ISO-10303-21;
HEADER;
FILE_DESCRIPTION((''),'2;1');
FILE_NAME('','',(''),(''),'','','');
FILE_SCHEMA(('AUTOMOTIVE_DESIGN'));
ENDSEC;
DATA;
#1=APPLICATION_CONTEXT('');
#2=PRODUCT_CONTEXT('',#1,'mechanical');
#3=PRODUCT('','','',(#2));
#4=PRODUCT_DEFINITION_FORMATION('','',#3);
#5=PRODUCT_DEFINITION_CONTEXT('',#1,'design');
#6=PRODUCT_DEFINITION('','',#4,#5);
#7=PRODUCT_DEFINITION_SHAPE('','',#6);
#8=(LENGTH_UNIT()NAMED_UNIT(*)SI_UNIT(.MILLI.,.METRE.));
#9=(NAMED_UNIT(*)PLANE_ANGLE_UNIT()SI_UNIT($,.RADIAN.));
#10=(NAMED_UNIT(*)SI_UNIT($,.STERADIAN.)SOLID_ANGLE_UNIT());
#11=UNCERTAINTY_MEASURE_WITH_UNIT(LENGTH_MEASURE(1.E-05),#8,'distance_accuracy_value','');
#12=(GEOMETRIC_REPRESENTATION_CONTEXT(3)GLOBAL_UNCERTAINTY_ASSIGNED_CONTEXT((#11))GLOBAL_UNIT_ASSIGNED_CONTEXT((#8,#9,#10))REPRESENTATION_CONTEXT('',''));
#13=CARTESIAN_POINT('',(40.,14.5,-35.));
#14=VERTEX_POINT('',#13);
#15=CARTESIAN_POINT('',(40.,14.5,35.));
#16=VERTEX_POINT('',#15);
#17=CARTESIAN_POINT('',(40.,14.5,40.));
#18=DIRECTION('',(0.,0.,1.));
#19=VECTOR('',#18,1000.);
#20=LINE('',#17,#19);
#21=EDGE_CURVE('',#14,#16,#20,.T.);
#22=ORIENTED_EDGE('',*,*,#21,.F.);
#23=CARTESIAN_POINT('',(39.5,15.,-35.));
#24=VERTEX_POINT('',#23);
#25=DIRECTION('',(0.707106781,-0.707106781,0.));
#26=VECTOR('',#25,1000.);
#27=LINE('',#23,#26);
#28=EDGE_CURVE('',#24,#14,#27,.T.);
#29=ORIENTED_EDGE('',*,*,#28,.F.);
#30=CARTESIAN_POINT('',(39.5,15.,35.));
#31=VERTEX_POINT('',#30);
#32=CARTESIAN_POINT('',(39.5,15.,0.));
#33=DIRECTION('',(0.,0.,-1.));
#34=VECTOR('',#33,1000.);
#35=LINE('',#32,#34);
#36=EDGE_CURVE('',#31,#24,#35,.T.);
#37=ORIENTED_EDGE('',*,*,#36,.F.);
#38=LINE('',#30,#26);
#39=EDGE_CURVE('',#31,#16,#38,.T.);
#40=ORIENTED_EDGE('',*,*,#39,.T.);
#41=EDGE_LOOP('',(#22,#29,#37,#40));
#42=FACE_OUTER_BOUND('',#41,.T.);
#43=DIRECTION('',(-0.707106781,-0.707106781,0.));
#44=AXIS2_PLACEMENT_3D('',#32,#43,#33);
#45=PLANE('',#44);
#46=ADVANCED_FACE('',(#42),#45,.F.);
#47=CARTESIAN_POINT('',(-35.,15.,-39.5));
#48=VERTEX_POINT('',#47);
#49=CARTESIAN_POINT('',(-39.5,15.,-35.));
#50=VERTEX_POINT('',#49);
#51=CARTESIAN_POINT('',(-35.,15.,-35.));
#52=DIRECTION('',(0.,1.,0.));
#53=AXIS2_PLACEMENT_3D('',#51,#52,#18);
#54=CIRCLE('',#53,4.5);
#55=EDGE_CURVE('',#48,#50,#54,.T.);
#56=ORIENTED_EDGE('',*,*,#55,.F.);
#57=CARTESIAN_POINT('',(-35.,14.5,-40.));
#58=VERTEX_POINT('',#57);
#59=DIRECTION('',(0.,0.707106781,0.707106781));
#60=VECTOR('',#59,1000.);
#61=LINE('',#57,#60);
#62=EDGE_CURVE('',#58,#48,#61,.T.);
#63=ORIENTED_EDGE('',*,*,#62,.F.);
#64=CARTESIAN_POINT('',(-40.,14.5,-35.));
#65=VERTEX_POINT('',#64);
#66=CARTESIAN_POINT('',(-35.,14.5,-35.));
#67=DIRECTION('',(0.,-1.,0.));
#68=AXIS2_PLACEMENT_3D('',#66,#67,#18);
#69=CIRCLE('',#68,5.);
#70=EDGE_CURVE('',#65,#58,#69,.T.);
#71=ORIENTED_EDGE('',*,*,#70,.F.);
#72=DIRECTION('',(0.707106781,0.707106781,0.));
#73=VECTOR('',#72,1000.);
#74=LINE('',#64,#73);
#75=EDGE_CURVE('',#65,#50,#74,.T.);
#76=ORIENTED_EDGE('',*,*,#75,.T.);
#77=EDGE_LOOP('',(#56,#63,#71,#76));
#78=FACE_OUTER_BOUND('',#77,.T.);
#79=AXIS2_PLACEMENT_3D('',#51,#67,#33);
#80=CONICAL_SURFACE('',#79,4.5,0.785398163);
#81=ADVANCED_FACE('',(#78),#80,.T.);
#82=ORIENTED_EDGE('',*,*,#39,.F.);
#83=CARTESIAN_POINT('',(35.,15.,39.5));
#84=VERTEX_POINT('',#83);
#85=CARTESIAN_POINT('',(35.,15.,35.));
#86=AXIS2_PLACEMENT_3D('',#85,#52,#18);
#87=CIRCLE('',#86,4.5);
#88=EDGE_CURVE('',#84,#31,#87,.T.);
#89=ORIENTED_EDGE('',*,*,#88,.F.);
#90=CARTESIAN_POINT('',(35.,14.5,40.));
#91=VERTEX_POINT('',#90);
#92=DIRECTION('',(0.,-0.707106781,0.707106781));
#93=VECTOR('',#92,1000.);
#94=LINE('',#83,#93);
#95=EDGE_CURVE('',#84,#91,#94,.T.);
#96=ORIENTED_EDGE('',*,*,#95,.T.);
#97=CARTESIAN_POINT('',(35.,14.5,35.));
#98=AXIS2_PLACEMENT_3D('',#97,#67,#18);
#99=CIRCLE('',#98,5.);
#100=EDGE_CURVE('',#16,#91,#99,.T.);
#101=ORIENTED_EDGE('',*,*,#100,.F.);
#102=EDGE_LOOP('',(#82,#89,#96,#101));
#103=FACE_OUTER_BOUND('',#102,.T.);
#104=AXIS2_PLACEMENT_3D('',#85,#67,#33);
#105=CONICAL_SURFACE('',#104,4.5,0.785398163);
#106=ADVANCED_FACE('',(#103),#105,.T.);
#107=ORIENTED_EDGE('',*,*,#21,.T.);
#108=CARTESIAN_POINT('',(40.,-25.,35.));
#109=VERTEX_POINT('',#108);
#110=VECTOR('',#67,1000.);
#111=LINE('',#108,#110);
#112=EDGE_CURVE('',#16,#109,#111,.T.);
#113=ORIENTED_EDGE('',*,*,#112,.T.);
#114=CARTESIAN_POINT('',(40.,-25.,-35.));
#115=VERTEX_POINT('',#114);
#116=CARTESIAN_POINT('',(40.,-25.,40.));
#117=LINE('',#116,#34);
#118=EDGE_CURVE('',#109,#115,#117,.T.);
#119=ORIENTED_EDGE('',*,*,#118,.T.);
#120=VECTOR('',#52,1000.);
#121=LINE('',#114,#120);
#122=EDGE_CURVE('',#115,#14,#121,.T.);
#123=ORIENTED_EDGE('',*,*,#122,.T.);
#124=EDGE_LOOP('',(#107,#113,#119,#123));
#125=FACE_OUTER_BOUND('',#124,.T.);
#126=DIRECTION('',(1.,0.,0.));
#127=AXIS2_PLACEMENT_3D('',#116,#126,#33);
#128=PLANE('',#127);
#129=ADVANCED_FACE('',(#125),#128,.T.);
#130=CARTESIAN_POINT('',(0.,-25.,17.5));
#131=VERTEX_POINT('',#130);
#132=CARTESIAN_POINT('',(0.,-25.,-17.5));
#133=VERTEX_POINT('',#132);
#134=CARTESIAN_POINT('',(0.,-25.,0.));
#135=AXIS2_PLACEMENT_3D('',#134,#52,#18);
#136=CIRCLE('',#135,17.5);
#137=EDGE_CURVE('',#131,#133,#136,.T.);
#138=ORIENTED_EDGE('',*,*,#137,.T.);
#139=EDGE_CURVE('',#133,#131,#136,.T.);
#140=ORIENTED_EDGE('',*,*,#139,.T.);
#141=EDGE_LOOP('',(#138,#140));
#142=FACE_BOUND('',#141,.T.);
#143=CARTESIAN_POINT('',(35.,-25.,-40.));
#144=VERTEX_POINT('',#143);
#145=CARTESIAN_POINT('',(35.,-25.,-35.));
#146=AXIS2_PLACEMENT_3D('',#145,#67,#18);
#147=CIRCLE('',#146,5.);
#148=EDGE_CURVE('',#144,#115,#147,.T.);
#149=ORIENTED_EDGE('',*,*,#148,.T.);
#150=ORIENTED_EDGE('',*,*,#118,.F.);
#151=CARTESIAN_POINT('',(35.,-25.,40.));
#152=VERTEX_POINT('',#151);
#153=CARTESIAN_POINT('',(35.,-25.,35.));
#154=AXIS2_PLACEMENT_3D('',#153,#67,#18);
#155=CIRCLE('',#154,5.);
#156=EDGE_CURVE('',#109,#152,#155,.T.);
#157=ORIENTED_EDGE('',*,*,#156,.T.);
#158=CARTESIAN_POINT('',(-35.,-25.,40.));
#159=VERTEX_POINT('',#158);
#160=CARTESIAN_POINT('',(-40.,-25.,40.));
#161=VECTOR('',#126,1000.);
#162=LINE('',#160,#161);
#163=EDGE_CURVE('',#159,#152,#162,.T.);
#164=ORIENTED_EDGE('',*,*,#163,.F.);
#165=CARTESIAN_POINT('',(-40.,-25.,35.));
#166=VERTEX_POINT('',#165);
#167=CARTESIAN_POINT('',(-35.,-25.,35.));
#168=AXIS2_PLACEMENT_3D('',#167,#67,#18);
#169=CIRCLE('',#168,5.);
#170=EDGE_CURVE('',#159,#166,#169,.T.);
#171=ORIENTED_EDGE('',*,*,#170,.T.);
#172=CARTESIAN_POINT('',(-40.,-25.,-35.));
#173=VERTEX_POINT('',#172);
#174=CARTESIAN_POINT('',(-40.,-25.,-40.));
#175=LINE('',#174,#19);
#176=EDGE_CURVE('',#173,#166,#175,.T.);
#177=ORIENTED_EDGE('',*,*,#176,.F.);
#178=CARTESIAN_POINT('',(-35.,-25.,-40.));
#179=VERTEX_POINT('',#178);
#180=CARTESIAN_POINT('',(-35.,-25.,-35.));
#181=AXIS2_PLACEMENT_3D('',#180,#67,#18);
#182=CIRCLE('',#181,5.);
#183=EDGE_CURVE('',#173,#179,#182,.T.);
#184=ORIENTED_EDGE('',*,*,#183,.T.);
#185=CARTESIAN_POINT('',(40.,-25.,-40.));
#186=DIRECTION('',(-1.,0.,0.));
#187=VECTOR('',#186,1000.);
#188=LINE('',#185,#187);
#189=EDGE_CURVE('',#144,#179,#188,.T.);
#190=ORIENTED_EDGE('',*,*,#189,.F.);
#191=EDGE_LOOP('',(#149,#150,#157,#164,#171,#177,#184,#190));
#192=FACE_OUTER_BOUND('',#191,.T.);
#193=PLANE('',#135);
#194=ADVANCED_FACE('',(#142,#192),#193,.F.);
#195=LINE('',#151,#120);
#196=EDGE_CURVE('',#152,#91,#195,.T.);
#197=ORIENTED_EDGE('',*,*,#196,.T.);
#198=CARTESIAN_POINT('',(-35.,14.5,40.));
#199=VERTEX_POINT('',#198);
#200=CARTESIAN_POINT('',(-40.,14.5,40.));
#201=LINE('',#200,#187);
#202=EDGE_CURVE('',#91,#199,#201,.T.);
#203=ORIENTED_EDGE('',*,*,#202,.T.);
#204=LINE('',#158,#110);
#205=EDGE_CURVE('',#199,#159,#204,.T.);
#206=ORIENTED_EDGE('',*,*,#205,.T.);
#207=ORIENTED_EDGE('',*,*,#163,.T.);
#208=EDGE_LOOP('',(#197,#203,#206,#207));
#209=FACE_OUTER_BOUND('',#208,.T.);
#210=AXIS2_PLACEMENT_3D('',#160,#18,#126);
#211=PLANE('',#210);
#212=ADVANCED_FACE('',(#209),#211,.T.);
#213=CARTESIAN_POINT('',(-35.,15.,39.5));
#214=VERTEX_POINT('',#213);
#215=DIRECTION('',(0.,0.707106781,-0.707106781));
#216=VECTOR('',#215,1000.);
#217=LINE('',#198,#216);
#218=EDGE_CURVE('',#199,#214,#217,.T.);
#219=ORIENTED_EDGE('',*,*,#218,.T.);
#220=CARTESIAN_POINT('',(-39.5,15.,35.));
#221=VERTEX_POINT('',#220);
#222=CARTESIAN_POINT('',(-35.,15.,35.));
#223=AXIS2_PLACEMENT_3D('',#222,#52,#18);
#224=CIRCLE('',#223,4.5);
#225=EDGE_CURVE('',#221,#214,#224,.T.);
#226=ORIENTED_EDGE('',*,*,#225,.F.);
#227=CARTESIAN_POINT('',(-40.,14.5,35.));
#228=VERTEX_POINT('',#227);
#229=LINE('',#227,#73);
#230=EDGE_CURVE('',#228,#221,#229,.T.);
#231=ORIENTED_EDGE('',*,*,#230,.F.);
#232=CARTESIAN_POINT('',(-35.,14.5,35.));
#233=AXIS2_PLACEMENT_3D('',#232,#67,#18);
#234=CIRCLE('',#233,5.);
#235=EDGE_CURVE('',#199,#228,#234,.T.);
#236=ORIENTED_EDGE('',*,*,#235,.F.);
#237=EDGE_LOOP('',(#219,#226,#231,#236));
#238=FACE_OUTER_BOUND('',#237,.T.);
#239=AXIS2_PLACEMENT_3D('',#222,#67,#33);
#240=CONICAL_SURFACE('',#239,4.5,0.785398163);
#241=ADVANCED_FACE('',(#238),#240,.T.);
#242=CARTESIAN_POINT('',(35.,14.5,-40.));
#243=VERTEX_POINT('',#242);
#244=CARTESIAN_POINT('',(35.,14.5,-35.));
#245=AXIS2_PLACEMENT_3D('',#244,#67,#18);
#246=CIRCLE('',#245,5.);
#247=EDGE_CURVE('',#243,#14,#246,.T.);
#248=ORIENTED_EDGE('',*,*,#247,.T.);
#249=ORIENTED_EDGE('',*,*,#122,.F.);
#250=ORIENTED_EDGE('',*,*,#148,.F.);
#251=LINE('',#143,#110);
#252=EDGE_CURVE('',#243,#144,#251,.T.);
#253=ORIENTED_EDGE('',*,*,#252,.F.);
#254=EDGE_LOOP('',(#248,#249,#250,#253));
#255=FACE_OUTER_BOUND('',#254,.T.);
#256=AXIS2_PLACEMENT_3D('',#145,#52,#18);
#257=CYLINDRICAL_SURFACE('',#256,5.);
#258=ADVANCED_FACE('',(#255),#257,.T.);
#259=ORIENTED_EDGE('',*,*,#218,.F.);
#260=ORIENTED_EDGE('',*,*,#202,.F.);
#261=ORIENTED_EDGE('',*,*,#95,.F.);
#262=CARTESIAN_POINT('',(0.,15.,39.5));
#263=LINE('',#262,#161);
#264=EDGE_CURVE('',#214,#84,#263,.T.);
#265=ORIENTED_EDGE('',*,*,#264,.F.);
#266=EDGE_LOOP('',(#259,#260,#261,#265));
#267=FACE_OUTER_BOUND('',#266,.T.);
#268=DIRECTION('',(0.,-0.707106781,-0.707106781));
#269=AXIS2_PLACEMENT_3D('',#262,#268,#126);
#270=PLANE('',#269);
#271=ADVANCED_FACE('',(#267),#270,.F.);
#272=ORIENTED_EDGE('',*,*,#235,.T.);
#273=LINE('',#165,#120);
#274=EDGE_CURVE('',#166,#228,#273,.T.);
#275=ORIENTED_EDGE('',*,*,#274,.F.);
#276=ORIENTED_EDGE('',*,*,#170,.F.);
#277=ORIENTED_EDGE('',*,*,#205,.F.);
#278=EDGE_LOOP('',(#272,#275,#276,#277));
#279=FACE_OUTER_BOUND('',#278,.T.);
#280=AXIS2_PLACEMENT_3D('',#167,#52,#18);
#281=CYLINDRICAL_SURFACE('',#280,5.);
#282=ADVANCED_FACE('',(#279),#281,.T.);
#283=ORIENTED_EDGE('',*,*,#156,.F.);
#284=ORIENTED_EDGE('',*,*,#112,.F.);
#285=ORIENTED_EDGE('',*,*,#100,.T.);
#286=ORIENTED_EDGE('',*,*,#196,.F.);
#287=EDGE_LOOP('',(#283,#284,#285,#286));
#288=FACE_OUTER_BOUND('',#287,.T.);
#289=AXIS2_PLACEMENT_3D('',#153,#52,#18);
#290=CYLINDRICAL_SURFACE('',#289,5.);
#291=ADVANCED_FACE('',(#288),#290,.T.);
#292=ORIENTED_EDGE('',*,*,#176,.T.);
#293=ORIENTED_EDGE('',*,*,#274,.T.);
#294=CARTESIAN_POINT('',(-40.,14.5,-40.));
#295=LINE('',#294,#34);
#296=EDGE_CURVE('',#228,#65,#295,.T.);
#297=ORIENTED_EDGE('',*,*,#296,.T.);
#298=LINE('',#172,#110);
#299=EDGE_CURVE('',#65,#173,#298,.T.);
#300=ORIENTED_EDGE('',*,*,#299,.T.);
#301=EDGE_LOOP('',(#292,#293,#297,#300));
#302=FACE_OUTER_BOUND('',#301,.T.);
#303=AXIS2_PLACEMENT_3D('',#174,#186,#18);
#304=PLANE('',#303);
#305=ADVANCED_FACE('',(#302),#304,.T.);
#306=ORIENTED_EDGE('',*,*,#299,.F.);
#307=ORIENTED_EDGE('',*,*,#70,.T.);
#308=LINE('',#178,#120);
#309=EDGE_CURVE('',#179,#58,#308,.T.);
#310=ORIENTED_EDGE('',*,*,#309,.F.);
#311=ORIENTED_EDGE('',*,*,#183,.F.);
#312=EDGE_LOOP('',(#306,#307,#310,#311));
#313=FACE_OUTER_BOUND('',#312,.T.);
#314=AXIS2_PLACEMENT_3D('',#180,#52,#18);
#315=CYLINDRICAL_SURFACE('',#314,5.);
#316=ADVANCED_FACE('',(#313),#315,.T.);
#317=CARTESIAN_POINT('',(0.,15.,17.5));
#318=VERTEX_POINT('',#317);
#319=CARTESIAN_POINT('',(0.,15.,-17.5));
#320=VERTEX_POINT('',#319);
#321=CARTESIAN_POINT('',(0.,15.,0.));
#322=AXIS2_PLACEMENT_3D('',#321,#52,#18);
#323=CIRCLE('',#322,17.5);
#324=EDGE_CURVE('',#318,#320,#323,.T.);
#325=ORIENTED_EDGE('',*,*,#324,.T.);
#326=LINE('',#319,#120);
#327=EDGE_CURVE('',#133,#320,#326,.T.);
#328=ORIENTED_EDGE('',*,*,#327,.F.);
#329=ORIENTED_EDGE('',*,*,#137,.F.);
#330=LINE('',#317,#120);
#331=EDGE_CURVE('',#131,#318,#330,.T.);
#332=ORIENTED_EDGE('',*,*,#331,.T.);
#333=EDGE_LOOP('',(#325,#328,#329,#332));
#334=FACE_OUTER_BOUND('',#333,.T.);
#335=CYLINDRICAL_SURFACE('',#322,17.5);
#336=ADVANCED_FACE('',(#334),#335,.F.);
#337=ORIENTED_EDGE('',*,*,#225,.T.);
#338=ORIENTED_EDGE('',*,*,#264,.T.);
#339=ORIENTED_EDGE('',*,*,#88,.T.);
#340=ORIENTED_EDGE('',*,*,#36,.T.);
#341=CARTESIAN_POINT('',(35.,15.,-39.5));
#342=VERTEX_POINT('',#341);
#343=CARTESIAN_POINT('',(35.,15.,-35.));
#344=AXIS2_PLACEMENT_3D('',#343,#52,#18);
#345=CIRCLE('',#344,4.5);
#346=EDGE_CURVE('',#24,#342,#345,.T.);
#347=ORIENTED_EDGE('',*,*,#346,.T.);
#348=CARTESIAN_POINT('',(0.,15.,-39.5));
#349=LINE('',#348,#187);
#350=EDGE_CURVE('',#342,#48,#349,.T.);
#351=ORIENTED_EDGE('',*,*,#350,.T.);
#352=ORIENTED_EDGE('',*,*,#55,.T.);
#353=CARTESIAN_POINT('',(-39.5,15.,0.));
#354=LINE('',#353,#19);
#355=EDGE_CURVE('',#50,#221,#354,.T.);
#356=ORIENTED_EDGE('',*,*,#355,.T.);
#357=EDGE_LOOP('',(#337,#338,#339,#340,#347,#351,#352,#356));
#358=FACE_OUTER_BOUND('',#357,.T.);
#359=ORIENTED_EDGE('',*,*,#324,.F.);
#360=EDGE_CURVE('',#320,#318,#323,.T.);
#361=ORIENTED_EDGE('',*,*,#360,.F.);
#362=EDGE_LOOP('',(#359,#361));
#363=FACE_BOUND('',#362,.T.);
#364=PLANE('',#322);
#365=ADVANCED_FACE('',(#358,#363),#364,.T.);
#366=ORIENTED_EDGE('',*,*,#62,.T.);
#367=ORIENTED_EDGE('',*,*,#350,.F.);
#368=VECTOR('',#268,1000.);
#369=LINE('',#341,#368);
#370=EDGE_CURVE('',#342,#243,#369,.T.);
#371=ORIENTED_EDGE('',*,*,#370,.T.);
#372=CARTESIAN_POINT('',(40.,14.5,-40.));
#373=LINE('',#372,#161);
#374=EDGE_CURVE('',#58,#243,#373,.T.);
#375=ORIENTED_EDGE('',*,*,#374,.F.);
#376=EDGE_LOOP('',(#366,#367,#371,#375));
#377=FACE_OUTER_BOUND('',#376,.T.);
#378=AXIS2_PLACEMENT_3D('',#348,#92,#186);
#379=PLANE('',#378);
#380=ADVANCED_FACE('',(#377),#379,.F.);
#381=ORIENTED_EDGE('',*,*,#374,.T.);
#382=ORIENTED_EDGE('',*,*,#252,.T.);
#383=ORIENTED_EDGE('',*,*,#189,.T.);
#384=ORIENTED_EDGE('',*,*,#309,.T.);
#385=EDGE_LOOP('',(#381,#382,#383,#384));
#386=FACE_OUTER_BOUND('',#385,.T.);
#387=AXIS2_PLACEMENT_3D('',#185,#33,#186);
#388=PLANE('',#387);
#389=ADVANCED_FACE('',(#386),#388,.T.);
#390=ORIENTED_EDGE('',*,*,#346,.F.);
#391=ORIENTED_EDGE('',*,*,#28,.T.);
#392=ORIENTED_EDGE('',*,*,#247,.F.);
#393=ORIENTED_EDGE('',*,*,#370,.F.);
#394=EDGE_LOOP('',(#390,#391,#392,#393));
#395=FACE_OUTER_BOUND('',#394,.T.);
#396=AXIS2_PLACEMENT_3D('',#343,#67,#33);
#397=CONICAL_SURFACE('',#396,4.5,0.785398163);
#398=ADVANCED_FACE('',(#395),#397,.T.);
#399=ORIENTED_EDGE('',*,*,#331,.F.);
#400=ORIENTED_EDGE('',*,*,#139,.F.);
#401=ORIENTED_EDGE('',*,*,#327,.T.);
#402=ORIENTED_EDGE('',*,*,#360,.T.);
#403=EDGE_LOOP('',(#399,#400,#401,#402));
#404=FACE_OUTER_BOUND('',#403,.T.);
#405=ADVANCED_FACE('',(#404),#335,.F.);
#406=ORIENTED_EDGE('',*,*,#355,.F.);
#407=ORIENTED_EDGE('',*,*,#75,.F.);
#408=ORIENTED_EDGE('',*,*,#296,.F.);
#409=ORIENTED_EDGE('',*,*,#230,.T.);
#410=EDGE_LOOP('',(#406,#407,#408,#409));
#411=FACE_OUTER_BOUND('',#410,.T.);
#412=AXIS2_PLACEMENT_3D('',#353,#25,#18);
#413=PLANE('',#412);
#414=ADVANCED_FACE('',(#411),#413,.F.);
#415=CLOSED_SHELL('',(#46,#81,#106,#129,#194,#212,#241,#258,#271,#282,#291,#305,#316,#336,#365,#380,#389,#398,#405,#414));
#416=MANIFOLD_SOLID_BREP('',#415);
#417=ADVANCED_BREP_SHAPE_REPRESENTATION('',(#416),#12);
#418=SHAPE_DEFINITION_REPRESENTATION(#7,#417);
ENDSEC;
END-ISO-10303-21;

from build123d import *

# Parameters (mm, degrees)
SKETCH1_W             = 80
SKETCH1_H             = 80
BOSS_EXTRUDE1_DEPTH   = 40
M30_CLEARANCE_HOLE1_D = 35
FILLET1_R             = 5
CHAMFER1_SIZE         = 0.5


with BuildPart() as part:
    # Sketch1 → Boss-Extrude1 (new body)
    with BuildSketch(Plane(origin=(0, 15, 0), x_dir=(1, 0, 0), z_dir=(0, 1, 0))):
        Rectangle(SKETCH1_W, SKETCH1_H)
    extrude(amount=-BOSS_EXTRUDE1_DEPTH)

    # M30 Clearance Hole1 (through all)
    with Locations(Plane(origin=(0, 15, 0), x_dir=(1, 0, 0), z_dir=(0, 1, 0))):
        with Locations((0, 0)):
            Hole(M30_CLEARANCE_HOLE1_D / 2)

    # Fillet1
    fillet1_edges = [part.edges().sort_by_distance(p)[0] for p in [
        (-40, -5, -40),
        (40, -5, -40),
        (40, -5, 40),
        (-40, -5, 40),
    ]]
    fillet(fillet1_edges, radius=FILLET1_R)

    # Chamfer1
    chamfer1_edges = [part.edges().sort_by_distance(p)[0] for p in [
        (0, 15, 40),
        (-40, 15, 0),
        (40, 15, 0),
        (0, 15, -40),
        (-38.535533906, 15, -38.535533906),
        (38.535533906, 15, -38.535533906),
        (-38.535533906, 15, 38.535533906),
        (38.535533906, 15, 38.535533906),
    ]]
    chamfer(chamfer1_edges, length=CHAMFER1_SIZE)


solid = part.part
